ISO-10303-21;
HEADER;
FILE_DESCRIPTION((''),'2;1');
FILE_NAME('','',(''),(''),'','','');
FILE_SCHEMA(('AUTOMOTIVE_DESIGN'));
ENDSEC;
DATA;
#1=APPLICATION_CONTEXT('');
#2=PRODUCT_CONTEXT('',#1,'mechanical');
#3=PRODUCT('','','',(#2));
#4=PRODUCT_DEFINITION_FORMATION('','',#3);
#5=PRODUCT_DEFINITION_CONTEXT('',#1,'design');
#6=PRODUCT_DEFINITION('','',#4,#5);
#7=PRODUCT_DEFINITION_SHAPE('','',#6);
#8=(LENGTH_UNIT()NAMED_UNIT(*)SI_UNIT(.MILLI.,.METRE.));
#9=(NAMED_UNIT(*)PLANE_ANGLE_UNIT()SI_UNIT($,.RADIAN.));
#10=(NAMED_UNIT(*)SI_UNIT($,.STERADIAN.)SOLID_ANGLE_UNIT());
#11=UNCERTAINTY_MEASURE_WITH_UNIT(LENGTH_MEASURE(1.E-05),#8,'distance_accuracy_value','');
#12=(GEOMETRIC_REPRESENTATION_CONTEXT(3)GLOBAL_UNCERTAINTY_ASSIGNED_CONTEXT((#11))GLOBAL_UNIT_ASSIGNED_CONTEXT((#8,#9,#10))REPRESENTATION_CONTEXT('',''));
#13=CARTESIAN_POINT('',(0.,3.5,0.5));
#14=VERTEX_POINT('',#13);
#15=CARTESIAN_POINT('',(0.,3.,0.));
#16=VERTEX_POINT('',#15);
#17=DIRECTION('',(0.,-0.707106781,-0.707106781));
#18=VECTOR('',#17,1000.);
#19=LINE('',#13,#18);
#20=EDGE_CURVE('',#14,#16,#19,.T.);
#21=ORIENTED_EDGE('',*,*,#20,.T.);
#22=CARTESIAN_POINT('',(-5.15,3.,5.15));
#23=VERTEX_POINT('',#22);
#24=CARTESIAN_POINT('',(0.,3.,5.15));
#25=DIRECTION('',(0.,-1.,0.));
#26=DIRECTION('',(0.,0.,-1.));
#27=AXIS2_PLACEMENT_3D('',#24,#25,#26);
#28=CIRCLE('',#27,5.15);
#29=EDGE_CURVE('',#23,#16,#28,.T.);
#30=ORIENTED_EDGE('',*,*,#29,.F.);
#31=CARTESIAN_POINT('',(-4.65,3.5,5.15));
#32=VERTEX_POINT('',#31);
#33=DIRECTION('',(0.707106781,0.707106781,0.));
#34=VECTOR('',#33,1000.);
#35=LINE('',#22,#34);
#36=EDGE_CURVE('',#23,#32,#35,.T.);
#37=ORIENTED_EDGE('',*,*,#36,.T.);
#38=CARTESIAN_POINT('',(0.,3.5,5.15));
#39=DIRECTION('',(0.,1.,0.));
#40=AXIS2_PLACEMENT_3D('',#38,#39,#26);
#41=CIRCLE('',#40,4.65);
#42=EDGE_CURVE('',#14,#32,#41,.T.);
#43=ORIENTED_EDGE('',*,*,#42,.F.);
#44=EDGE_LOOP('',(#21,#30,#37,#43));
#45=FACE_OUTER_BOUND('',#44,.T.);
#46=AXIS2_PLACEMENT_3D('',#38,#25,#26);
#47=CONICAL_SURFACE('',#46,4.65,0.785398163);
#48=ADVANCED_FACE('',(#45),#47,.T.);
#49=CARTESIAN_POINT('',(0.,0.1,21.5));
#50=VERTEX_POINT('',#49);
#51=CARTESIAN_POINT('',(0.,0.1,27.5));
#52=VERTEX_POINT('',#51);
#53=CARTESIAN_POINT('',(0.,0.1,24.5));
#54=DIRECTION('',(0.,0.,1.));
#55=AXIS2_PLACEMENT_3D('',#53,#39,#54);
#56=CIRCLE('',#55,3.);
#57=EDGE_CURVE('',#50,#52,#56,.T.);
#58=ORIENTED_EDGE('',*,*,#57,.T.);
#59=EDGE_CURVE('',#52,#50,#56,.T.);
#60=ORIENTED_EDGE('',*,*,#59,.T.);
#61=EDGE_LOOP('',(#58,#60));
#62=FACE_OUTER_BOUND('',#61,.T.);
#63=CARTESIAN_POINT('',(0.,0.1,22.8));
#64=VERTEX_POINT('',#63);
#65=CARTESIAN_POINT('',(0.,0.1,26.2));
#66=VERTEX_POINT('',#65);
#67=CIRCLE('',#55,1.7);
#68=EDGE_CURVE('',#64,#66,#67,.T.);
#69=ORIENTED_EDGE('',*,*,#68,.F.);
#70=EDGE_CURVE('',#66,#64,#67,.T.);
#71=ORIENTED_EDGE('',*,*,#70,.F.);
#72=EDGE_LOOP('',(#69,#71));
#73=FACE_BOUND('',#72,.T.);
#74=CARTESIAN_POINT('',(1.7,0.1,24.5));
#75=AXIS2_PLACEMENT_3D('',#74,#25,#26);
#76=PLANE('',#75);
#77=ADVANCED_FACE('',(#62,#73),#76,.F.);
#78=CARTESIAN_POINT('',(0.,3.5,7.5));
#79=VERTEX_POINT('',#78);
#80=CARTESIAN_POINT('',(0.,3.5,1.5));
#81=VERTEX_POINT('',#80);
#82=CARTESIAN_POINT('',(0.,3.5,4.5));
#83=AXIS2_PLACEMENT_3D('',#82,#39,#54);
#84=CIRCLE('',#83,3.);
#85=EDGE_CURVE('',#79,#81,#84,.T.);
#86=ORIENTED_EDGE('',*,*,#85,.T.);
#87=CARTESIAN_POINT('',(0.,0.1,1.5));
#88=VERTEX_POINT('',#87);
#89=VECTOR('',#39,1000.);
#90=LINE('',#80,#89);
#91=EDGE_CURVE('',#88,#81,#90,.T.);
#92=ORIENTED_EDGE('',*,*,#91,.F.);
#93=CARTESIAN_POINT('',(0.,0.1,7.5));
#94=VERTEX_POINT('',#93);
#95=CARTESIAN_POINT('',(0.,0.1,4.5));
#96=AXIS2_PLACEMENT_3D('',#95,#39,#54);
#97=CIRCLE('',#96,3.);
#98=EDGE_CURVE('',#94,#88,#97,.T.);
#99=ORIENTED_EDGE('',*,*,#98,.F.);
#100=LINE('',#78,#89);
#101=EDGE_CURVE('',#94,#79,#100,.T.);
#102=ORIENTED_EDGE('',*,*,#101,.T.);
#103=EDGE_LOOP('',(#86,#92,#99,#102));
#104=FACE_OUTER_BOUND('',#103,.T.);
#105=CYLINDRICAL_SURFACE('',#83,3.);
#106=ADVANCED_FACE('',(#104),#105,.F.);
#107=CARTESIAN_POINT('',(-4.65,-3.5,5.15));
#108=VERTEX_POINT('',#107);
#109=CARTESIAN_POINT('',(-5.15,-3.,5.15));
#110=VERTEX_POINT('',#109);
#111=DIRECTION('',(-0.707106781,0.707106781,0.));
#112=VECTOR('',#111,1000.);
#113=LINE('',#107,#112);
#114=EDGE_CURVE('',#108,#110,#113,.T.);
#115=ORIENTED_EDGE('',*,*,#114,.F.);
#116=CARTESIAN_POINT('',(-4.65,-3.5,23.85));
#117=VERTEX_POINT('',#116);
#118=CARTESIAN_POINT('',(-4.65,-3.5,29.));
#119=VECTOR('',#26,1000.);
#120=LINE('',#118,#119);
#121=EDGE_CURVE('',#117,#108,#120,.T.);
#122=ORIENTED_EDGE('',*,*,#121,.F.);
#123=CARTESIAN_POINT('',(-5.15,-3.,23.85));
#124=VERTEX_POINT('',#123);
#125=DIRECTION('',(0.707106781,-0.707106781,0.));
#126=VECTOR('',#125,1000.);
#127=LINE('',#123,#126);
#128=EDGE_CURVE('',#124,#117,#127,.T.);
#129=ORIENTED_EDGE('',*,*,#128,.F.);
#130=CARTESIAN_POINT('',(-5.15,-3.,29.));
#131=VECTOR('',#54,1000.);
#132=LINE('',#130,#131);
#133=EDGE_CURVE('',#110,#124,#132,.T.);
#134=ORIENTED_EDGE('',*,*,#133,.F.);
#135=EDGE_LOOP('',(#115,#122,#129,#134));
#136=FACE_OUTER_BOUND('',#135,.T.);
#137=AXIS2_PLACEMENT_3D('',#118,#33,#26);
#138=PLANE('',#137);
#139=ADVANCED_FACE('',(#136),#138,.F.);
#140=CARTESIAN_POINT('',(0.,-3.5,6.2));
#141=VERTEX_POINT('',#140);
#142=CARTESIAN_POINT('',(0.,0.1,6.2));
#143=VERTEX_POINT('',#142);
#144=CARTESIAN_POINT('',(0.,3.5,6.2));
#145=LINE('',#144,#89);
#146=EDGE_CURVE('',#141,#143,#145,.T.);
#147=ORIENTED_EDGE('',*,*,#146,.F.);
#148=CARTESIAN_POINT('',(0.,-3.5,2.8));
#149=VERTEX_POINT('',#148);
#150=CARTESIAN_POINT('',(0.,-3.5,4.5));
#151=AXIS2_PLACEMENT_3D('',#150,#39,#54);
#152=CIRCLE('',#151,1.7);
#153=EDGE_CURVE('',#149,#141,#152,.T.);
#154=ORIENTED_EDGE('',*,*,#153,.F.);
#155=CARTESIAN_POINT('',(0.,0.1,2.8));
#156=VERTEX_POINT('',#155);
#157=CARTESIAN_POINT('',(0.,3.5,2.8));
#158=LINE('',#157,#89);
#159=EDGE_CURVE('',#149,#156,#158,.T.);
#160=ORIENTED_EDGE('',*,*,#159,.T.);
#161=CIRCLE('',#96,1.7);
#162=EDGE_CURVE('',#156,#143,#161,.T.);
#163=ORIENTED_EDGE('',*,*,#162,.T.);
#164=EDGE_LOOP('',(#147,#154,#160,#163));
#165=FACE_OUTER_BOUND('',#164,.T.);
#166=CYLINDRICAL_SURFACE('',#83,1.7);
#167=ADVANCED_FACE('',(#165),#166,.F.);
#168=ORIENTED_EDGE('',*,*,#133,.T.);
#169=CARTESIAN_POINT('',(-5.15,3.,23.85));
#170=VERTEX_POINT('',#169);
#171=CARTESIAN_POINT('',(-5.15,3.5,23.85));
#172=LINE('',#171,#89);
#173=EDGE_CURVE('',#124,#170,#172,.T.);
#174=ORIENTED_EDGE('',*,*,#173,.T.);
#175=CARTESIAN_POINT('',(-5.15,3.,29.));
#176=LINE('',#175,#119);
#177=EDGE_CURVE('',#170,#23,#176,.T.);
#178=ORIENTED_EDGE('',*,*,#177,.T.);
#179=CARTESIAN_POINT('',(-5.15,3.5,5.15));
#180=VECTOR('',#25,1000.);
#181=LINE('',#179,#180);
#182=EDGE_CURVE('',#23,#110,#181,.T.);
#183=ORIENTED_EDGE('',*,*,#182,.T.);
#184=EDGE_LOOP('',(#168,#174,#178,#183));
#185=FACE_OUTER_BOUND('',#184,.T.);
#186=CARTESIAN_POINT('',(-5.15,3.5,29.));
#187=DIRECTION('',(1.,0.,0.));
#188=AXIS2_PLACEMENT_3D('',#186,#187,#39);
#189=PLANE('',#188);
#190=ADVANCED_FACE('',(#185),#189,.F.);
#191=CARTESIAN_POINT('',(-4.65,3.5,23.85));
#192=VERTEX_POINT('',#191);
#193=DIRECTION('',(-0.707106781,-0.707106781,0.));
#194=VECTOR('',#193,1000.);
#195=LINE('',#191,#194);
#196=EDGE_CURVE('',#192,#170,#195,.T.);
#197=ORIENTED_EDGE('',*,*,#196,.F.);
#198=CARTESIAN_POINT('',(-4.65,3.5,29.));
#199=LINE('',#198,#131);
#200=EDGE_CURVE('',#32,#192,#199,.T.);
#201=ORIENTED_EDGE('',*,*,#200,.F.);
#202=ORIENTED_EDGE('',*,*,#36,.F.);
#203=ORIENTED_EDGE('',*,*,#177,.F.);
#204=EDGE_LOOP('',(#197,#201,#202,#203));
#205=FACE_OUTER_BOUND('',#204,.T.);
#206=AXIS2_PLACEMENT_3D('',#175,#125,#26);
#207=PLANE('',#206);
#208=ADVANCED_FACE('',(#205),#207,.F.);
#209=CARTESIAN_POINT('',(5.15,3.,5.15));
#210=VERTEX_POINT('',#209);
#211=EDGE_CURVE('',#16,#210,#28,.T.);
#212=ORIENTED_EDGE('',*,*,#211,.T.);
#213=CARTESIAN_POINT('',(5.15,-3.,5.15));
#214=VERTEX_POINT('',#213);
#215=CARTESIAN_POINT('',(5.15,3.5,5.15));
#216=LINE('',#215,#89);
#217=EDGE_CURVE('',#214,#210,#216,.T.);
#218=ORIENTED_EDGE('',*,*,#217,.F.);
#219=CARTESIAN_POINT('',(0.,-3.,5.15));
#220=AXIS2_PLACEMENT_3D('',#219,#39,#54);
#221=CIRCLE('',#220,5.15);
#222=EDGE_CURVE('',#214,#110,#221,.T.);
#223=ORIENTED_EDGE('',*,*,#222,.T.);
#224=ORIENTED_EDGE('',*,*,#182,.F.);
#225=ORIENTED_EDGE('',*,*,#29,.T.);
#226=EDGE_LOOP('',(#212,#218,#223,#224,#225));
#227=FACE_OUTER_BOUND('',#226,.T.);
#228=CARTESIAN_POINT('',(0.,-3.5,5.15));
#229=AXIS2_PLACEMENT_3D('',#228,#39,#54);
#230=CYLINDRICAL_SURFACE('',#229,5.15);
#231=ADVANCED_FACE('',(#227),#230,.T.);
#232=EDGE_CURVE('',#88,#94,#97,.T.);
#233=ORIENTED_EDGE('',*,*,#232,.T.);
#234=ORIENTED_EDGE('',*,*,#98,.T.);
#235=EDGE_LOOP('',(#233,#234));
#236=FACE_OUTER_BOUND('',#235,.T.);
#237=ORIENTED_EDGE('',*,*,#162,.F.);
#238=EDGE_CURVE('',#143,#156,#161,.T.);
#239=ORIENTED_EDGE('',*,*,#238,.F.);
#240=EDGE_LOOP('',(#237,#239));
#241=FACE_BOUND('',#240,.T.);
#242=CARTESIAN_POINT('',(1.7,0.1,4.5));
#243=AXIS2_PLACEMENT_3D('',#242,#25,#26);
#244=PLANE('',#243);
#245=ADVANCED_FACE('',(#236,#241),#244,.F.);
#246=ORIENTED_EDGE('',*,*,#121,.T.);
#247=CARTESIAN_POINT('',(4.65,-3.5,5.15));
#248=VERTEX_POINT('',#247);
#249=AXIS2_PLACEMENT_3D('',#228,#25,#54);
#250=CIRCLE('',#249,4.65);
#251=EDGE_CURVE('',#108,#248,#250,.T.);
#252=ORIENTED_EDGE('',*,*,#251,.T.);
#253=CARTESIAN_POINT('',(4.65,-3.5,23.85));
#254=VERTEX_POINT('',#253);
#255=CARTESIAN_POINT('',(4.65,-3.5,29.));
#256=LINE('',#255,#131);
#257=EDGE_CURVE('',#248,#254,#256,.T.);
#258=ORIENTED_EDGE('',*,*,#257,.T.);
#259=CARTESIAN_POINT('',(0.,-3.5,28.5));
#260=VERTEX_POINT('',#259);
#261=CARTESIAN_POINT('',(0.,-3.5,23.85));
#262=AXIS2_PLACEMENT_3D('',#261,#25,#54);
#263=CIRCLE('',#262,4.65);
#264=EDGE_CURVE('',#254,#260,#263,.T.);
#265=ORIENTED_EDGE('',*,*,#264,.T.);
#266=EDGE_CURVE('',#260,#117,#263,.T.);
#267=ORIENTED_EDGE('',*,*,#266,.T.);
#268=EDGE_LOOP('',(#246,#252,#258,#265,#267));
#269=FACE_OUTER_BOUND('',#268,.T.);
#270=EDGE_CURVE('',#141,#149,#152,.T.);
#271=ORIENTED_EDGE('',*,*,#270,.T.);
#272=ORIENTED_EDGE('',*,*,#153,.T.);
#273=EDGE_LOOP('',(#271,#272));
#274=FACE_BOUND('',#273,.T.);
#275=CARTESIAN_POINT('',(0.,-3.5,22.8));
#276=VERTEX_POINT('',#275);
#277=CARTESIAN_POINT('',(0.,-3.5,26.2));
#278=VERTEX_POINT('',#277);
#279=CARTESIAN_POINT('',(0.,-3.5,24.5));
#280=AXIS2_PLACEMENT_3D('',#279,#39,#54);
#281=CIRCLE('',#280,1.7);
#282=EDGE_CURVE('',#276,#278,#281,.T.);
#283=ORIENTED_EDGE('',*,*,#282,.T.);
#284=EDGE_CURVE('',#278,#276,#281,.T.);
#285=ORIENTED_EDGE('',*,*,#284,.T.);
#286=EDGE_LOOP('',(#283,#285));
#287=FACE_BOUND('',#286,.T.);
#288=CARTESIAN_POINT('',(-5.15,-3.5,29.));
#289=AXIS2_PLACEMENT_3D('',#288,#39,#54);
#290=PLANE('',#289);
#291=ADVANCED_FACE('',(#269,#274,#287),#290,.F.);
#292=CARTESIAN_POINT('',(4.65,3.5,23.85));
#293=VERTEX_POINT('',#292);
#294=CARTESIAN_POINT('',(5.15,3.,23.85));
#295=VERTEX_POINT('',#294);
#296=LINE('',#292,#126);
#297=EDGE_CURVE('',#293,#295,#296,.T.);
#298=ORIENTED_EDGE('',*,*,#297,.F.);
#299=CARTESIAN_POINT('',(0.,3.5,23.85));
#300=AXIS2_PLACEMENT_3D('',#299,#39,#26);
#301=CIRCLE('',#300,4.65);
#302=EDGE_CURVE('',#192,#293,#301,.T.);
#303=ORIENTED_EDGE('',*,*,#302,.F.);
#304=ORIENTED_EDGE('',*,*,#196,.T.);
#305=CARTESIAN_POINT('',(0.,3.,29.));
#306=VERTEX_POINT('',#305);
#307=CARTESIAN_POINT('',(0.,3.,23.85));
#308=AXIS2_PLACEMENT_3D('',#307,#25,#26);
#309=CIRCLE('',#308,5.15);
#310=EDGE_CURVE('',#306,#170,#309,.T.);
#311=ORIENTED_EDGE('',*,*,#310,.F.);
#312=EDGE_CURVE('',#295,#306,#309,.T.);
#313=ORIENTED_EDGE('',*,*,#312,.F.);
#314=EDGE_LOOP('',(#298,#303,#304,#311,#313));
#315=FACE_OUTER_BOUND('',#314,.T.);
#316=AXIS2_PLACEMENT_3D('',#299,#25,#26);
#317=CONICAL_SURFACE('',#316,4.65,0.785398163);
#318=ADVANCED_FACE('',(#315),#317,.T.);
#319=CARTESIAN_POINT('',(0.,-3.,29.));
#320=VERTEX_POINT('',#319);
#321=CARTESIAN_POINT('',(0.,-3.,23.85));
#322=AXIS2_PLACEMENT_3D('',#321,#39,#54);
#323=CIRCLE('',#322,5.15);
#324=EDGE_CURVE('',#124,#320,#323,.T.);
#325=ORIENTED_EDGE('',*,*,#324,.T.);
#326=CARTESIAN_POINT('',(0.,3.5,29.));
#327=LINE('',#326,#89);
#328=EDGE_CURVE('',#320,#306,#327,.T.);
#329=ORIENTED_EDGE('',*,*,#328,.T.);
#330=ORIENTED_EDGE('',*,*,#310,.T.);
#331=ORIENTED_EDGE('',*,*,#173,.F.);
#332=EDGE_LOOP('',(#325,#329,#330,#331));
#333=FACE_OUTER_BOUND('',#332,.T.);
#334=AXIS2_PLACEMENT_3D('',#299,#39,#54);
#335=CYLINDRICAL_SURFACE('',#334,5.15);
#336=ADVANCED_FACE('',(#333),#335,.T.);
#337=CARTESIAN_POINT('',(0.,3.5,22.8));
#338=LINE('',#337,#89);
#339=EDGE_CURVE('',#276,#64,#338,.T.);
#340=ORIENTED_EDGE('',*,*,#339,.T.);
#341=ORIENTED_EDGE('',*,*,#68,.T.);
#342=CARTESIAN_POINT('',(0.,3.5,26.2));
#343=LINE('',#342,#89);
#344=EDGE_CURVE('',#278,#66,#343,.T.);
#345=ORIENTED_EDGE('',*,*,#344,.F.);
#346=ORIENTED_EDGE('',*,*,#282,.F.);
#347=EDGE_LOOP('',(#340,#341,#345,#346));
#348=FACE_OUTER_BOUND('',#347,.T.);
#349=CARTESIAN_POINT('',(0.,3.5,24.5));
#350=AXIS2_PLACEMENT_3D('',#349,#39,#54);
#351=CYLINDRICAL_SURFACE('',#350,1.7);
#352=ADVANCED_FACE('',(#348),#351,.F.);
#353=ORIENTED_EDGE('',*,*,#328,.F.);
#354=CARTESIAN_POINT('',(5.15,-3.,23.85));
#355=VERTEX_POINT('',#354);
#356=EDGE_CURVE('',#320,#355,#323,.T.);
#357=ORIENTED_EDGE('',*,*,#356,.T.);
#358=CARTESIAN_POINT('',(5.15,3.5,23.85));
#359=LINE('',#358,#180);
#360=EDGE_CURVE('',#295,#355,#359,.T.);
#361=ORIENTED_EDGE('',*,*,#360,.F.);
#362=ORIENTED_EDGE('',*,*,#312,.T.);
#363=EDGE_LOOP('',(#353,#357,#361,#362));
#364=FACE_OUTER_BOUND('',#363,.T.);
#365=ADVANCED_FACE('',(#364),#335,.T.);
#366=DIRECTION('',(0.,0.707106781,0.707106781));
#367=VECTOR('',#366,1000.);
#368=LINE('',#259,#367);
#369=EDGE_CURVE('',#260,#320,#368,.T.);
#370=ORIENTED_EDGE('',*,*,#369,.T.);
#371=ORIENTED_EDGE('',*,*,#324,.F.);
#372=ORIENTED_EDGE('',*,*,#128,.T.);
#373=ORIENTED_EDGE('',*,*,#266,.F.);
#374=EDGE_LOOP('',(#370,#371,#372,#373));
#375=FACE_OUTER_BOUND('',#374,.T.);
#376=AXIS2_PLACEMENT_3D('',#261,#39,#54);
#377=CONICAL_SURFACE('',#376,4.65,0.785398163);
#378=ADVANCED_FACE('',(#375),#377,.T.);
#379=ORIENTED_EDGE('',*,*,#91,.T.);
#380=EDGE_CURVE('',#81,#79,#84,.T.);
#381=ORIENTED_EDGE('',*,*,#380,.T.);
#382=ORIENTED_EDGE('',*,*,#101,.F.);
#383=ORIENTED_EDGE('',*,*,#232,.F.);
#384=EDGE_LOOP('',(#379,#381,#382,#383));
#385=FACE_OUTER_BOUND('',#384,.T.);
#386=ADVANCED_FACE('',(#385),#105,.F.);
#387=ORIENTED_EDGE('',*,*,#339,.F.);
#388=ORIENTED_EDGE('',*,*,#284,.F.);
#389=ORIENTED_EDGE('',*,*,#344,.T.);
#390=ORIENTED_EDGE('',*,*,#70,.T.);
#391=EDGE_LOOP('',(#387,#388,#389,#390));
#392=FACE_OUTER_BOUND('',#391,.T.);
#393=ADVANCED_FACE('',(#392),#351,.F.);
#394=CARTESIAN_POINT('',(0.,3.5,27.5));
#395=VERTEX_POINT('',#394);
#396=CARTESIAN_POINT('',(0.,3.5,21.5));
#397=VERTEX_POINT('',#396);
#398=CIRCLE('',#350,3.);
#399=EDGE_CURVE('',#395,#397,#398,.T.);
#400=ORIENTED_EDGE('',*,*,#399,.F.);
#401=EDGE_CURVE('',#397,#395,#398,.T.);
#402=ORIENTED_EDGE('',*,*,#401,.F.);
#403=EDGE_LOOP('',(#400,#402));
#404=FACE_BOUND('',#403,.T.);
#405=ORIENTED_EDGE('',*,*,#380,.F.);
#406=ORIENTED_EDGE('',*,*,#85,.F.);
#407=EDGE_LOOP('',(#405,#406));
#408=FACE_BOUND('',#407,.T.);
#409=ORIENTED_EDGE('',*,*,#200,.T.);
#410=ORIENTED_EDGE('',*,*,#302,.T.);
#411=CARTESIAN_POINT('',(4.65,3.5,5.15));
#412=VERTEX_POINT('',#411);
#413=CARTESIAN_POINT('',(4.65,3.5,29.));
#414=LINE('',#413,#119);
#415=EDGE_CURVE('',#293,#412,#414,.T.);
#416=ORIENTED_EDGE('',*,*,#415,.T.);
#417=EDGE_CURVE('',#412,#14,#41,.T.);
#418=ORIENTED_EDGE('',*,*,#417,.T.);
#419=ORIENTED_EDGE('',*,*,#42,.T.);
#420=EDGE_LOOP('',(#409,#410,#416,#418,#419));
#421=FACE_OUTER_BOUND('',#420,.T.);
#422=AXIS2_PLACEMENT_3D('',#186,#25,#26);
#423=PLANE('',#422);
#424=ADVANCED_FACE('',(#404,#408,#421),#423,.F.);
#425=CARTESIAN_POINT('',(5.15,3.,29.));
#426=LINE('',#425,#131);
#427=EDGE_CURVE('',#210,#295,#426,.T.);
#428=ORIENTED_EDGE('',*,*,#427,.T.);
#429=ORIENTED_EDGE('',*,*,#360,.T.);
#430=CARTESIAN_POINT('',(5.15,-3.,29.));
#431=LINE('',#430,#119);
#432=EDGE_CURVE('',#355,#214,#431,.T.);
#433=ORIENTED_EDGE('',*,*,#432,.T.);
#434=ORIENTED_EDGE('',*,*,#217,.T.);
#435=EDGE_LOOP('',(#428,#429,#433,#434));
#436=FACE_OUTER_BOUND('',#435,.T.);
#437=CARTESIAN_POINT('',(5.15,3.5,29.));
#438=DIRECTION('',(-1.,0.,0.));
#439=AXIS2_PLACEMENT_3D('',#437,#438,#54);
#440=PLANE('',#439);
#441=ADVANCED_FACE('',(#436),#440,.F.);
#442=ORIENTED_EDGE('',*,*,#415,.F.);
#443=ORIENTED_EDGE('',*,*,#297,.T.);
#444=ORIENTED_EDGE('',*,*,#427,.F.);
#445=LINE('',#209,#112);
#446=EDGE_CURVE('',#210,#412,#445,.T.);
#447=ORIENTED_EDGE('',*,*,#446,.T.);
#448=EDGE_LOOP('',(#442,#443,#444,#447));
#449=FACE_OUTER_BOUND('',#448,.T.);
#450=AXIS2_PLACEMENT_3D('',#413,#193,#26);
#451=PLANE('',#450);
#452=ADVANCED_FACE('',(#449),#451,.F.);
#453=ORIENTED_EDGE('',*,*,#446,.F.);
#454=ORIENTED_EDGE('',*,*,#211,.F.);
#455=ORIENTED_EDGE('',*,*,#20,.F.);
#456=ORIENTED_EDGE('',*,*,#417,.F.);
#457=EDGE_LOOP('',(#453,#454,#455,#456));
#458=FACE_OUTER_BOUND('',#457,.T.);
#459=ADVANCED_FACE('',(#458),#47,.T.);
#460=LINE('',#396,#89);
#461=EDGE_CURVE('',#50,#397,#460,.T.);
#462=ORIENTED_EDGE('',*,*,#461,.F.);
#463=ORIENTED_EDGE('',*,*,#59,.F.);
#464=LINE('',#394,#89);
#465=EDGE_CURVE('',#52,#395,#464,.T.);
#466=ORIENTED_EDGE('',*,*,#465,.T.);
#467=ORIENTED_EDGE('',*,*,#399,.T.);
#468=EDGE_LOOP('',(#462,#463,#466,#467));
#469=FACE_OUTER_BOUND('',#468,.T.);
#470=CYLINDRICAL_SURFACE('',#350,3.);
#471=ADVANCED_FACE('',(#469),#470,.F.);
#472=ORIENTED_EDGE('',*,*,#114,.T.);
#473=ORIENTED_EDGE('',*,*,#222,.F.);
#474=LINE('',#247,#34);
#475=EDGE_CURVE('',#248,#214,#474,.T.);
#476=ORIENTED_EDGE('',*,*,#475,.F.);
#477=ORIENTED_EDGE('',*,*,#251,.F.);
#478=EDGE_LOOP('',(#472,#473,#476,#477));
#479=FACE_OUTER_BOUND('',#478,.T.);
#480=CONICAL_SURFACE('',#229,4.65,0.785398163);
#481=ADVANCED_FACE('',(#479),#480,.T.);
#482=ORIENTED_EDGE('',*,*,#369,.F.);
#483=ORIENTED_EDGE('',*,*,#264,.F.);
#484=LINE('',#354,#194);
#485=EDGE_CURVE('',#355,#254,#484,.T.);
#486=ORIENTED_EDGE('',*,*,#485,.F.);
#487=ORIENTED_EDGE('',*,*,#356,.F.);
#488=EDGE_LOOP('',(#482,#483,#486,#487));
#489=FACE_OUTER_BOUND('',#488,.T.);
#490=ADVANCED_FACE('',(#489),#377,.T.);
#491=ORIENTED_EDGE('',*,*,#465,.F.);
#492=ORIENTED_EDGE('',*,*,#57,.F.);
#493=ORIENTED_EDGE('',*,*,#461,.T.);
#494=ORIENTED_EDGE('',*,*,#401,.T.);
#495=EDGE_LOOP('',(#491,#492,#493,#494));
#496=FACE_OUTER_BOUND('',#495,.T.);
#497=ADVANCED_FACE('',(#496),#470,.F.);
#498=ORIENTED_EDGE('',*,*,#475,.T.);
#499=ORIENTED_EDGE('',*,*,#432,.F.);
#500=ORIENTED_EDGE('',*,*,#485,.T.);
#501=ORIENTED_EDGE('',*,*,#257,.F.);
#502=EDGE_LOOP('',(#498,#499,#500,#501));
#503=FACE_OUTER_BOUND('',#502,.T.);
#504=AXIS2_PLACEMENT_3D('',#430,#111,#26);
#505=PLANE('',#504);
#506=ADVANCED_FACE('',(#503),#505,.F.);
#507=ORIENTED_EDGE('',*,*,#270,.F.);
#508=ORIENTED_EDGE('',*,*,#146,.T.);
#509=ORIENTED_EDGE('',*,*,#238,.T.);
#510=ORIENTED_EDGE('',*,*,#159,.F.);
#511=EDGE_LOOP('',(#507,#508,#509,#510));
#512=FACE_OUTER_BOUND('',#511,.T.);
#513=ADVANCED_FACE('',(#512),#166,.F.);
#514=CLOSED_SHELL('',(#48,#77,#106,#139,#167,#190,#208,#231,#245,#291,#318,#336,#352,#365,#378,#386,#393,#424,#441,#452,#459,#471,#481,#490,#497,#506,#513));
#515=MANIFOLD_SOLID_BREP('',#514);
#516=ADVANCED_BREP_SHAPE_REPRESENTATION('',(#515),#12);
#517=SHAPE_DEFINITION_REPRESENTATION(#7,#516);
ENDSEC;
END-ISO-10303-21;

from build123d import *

# Parameters (mm, degrees)
SKETCH1_W                                           = 10.3
SKETCH1_H                                           = 7
BOSS_EXTRUDE1_DEPTH                                 = 29
FILLET1_RADIUS                                      = 5.15
FILLET1_LENGTH                                      = 7
FILLET2_RADIUS                                      = 5.15
FILLET2_LENGTH                                      = 7
CHAMFER1_SIZE                                       = 0.5
HOLE_SPEC_PER_SOCKET_HEAD_CAP_SCREW_TYP_D           = 3.4
HOLE_SPEC_PER_SOCKET_HEAD_CAP_SCREW_TYP_CBORE_D     = 6
HOLE_SPEC_PER_SOCKET_HEAD_CAP_SCREW_TYP_CBORE_DEPTH = 3.4


with BuildPart() as part:
    # Sketch1 → Boss-Extrude1 (new body)
    with BuildSketch(Plane.XY):
        Rectangle(SKETCH1_W, SKETCH1_H)
    extrude(amount=BOSS_EXTRUDE1_DEPTH)

    # Fillet1: full round fillet: the end face becomes a half cylinder, R = half its width
    fillet1_face = Plane((0, 0, 0), x_dir=(0, 1, 0), z_dir=(0, 0, -1))  # on the end face: x along it, z out of the body
    fillet1_slab = fillet1_face.offset(-FILLET1_RADIUS / 2) * Box(FILLET1_LENGTH, 2 * FILLET1_RADIUS, FILLET1_RADIUS, mode=Mode.PRIVATE)  # the body's end, R deep
    fillet1_round = Plane((0, 0, 5.15), x_dir=(0, 0, -1), z_dir=(0, 1, 0)) * Cylinder(FILLET1_RADIUS, FILLET1_LENGTH, mode=Mode.PRIVATE)  # its axis R under the face
    add(fillet1_slab - fillet1_round, mode=Mode.SUBTRACT)

    # Fillet2: full round fillet: the end face becomes a half cylinder, R = half its width
    fillet2_face = Plane((0, 0, 29), x_dir=(0, -1, 0), z_dir=(0, 0, 1))  # on the end face: x along it, z out of the body
    fillet2_slab = fillet2_face.offset(-FILLET2_RADIUS / 2) * Box(FILLET2_LENGTH, 2 * FILLET2_RADIUS, FILLET2_RADIUS, mode=Mode.PRIVATE)  # the body's end, R deep
    fillet2_round = Plane((0, 0, 23.85), x_dir=(0, 0, 1), z_dir=(0, -1, 0)) * Cylinder(FILLET2_RADIUS, FILLET2_LENGTH, mode=Mode.PRIVATE)  # its axis R under the face
    add(fillet2_slab - fillet2_round, mode=Mode.SUBTRACT)

    # Chamfer1
    chamfer1_edges = [part.edges().sort_by_distance(p)[0] for p in [
        (0, -3.5, 0),
        (0, 3.5, 0),
        (5.15, -3.5, 14.5),
        (5.15, 3.5, 14.5),
        (-5.15, 3.5, 14.5),
        (-5.15, -3.5, 14.5),
        (0, 3.5, 29),
        (0, -3.5, 29),
    ]]
    chamfer(chamfer1_edges, length=CHAMFER1_SIZE)

    # Hole Spec (per socket head cap screw type) 1 (through all)
    with Locations(Plane(origin=(0, 3.5, 0), x_dir=(1, 0, 0), z_dir=(0, 1, 0))):
        with Locations((0, -24.5), (0, -4.5)):
            CounterBoreHole(HOLE_SPEC_PER_SOCKET_HEAD_CAP_SCREW_TYP_D / 2, HOLE_SPEC_PER_SOCKET_HEAD_CAP_SCREW_TYP_CBORE_D / 2, HOLE_SPEC_PER_SOCKET_HEAD_CAP_SCREW_TYP_CBORE_DEPTH)


solid = part.part
